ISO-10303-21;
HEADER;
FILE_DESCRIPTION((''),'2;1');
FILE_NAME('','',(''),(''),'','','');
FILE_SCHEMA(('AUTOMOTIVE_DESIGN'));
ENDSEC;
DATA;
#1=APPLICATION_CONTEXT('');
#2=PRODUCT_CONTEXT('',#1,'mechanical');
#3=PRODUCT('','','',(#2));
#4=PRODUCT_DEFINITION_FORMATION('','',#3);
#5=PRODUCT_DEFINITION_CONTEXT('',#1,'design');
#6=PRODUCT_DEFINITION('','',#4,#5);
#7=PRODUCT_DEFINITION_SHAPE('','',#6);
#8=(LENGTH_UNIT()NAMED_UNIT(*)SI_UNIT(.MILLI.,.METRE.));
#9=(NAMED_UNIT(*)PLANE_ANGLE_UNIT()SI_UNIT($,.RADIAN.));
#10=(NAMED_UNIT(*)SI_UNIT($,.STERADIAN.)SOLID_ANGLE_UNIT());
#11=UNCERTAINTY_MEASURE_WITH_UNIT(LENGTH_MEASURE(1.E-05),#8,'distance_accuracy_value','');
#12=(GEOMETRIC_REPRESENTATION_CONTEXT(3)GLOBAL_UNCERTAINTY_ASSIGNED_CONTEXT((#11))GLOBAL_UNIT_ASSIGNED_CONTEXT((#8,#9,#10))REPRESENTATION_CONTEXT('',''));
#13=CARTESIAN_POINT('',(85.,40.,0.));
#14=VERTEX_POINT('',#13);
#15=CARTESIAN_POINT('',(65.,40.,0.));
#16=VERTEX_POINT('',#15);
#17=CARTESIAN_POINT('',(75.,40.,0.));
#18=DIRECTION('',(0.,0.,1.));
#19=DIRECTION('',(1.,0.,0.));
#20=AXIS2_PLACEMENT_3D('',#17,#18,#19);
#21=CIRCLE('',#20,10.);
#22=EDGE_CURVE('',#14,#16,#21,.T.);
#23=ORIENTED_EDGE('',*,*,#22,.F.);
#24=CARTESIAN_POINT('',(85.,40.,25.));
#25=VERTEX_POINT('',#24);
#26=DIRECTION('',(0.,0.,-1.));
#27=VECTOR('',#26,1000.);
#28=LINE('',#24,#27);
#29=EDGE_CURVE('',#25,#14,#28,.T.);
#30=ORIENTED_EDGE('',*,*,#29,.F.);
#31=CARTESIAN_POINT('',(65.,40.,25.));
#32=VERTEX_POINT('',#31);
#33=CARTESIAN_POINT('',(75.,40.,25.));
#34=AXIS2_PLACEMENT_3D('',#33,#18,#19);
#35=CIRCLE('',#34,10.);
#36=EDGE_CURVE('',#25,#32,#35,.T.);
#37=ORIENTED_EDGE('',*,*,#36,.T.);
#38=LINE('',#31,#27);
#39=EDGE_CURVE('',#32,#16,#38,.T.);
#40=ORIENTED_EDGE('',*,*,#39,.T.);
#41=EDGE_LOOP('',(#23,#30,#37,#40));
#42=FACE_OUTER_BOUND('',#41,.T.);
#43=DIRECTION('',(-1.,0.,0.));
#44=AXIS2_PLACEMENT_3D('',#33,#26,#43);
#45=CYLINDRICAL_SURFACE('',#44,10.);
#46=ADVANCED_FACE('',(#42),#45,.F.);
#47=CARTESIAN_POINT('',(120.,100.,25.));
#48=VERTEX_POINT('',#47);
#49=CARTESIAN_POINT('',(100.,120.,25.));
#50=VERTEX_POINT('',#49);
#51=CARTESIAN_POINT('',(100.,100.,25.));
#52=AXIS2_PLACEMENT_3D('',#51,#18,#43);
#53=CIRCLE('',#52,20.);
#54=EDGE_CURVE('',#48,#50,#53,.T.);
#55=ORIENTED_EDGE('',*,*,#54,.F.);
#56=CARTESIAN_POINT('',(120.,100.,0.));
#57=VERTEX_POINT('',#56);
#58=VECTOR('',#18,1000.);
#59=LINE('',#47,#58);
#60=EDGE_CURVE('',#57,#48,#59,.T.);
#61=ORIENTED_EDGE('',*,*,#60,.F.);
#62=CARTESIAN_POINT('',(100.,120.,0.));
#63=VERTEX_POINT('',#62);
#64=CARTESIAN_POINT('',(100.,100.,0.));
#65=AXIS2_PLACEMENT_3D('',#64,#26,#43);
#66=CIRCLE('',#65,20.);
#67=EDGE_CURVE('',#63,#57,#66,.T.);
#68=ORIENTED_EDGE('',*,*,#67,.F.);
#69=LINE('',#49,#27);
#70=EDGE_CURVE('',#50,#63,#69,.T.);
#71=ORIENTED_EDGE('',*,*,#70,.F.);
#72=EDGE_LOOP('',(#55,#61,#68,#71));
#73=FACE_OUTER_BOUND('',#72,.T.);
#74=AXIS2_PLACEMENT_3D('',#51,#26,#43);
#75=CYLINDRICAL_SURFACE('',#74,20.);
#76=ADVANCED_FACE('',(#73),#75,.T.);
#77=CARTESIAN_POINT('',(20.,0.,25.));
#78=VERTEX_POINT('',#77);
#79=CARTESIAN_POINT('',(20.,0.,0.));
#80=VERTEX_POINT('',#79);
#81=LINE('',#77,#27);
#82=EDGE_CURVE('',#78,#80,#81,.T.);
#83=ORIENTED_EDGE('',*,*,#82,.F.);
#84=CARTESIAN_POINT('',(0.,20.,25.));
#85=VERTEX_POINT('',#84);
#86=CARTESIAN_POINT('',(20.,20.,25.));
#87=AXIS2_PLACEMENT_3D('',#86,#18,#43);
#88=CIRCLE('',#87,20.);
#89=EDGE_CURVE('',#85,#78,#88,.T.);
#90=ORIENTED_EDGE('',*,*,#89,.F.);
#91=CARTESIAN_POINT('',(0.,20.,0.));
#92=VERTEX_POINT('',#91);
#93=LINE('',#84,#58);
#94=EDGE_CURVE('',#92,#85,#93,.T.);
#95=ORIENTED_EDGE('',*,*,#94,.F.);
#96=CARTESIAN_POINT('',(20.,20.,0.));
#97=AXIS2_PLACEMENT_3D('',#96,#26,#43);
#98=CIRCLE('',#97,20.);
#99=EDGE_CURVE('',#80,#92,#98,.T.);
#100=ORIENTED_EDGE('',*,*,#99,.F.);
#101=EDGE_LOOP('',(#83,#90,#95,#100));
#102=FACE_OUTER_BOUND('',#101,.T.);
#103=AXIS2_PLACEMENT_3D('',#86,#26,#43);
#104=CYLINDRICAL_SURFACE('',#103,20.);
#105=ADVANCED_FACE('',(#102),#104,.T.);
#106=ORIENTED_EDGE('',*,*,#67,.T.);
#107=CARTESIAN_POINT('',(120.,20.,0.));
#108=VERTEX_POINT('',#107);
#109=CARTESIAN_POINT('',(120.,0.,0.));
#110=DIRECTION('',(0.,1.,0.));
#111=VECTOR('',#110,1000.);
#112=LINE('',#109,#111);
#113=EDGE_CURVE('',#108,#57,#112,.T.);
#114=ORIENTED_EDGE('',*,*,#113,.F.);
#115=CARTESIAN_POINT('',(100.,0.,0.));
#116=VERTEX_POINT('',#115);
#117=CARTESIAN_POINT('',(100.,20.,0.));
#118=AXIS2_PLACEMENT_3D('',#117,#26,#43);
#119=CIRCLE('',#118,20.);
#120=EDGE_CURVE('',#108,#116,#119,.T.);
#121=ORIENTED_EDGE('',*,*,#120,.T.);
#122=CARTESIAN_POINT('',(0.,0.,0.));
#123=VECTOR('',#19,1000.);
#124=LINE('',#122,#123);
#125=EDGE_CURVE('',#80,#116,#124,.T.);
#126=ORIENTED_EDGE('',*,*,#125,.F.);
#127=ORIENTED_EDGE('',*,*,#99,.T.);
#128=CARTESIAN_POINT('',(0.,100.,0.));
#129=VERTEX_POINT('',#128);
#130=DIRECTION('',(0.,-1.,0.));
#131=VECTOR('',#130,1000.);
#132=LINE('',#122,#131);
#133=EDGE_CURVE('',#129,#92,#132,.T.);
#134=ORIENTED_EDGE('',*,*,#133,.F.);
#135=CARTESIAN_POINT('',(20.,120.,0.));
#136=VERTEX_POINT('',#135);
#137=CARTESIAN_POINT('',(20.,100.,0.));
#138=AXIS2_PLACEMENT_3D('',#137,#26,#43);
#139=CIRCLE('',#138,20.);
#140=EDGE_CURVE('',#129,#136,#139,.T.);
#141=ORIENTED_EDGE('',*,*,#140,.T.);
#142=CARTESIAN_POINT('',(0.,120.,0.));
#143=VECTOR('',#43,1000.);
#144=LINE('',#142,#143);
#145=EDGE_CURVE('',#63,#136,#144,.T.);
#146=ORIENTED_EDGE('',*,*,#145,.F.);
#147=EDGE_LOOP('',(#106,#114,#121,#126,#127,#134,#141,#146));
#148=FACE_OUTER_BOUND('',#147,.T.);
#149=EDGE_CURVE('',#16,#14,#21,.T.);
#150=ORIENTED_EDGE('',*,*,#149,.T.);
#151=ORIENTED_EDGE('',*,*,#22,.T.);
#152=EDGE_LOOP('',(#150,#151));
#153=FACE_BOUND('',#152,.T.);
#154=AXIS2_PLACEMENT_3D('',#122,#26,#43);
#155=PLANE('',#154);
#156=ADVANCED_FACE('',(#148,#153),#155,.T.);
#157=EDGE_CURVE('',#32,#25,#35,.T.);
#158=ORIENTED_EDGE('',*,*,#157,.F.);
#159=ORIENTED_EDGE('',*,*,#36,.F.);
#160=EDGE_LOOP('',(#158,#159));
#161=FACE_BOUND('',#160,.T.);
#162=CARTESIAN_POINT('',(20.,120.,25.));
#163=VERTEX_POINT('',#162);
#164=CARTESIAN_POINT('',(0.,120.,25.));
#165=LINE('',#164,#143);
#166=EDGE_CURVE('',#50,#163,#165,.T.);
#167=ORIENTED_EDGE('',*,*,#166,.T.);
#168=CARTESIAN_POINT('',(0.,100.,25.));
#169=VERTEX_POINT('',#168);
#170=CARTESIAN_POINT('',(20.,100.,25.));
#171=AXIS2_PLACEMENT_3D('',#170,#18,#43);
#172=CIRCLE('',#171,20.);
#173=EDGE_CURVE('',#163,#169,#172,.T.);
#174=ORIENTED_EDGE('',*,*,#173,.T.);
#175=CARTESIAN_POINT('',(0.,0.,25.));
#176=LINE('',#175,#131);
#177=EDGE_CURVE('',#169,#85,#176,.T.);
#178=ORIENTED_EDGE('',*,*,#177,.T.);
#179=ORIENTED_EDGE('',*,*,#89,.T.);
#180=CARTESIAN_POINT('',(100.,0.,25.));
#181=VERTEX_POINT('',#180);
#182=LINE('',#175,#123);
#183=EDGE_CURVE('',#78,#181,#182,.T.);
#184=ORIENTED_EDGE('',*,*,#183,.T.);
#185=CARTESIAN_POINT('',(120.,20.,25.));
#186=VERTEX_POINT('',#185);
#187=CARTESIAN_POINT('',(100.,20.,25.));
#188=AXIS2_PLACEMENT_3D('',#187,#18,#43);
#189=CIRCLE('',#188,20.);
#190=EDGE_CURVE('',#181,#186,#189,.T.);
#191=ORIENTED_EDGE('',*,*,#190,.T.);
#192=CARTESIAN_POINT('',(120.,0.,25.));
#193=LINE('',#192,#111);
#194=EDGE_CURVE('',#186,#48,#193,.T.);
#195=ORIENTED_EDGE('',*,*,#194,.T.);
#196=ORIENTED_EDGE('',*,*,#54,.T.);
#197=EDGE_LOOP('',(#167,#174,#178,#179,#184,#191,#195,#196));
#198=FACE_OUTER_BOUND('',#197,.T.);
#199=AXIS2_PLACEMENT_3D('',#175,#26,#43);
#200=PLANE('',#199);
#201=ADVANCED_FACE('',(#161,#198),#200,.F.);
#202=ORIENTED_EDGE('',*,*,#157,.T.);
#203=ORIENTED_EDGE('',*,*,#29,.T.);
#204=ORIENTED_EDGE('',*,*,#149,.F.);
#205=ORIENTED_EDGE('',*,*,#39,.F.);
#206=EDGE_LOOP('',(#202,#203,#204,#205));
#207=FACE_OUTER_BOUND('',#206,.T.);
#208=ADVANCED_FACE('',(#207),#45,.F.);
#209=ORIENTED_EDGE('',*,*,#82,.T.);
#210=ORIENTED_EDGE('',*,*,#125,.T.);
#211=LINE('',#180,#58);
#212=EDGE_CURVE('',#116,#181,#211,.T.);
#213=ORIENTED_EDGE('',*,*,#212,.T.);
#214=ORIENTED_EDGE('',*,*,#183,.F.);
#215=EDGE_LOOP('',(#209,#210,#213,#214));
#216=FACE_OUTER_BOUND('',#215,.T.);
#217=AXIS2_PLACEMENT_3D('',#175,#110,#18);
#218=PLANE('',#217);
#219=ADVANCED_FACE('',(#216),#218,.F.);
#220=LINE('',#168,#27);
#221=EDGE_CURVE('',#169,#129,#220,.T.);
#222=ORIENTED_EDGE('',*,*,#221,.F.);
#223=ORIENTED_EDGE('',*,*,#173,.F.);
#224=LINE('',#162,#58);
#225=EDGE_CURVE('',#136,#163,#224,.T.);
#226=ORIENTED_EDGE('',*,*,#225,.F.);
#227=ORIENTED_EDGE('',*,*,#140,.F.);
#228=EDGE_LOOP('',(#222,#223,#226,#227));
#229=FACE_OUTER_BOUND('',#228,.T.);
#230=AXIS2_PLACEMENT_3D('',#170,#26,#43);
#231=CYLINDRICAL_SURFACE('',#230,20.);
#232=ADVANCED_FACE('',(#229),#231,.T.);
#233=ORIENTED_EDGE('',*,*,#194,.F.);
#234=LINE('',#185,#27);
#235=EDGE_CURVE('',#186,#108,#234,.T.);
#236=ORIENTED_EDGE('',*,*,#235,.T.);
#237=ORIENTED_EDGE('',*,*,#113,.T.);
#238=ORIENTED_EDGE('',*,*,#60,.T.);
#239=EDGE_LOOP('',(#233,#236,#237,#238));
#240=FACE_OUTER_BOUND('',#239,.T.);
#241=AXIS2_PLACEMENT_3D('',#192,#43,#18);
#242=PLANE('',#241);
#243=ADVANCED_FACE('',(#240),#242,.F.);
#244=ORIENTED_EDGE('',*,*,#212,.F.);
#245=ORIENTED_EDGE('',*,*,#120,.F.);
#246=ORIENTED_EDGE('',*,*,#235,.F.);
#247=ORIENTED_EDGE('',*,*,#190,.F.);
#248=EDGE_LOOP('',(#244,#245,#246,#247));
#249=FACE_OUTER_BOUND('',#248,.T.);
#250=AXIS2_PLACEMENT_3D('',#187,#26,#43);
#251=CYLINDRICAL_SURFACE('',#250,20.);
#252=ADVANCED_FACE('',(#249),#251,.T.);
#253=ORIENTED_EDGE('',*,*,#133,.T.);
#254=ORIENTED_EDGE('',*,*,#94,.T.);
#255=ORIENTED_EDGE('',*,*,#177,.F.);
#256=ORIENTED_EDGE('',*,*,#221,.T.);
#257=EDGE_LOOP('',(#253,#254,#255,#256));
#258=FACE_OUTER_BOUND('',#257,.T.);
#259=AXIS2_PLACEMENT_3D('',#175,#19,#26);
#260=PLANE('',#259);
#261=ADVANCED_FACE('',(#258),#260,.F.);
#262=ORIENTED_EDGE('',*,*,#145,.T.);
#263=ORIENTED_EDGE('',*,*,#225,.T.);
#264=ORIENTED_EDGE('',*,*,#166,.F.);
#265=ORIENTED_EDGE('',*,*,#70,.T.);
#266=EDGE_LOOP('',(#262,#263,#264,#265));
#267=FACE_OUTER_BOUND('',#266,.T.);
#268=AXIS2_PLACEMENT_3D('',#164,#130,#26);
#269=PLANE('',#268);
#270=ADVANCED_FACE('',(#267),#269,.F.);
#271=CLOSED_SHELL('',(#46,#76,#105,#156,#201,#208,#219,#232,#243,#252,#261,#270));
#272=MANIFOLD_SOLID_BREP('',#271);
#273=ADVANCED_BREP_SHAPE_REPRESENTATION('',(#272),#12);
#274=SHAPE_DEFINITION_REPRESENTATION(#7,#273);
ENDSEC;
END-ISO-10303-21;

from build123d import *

# Parameters (mm, degrees)
SKETCH1_W           = 120
SKETCH1_H           = 120
SKETCH1_R           = 10
BOSS_EXTRUDE1_DEPTH = 25
FILLET1_R           = 20


with BuildPart() as part:
    # Sketch1 → Boss-Extrude1 (new body)
    with BuildSketch(Plane.XY):
        with Locations((60, 60)):
            Rectangle(SKETCH1_W, SKETCH1_H)
        with Locations((75, 40)):
            Circle(SKETCH1_R, mode=Mode.SUBTRACT)
    extrude(amount=BOSS_EXTRUDE1_DEPTH)

    # Fillet1
    fillet1_edges = [part.edges().sort_by_distance(p)[0] for p in [
        (0, 120, 12.5),
        (120, 120, 12.5),
        (120, 0, 12.5),
        (0, 0, 12.5),
    ]]
    fillet(fillet1_edges, radius=FILLET1_R)


solid = part.part
